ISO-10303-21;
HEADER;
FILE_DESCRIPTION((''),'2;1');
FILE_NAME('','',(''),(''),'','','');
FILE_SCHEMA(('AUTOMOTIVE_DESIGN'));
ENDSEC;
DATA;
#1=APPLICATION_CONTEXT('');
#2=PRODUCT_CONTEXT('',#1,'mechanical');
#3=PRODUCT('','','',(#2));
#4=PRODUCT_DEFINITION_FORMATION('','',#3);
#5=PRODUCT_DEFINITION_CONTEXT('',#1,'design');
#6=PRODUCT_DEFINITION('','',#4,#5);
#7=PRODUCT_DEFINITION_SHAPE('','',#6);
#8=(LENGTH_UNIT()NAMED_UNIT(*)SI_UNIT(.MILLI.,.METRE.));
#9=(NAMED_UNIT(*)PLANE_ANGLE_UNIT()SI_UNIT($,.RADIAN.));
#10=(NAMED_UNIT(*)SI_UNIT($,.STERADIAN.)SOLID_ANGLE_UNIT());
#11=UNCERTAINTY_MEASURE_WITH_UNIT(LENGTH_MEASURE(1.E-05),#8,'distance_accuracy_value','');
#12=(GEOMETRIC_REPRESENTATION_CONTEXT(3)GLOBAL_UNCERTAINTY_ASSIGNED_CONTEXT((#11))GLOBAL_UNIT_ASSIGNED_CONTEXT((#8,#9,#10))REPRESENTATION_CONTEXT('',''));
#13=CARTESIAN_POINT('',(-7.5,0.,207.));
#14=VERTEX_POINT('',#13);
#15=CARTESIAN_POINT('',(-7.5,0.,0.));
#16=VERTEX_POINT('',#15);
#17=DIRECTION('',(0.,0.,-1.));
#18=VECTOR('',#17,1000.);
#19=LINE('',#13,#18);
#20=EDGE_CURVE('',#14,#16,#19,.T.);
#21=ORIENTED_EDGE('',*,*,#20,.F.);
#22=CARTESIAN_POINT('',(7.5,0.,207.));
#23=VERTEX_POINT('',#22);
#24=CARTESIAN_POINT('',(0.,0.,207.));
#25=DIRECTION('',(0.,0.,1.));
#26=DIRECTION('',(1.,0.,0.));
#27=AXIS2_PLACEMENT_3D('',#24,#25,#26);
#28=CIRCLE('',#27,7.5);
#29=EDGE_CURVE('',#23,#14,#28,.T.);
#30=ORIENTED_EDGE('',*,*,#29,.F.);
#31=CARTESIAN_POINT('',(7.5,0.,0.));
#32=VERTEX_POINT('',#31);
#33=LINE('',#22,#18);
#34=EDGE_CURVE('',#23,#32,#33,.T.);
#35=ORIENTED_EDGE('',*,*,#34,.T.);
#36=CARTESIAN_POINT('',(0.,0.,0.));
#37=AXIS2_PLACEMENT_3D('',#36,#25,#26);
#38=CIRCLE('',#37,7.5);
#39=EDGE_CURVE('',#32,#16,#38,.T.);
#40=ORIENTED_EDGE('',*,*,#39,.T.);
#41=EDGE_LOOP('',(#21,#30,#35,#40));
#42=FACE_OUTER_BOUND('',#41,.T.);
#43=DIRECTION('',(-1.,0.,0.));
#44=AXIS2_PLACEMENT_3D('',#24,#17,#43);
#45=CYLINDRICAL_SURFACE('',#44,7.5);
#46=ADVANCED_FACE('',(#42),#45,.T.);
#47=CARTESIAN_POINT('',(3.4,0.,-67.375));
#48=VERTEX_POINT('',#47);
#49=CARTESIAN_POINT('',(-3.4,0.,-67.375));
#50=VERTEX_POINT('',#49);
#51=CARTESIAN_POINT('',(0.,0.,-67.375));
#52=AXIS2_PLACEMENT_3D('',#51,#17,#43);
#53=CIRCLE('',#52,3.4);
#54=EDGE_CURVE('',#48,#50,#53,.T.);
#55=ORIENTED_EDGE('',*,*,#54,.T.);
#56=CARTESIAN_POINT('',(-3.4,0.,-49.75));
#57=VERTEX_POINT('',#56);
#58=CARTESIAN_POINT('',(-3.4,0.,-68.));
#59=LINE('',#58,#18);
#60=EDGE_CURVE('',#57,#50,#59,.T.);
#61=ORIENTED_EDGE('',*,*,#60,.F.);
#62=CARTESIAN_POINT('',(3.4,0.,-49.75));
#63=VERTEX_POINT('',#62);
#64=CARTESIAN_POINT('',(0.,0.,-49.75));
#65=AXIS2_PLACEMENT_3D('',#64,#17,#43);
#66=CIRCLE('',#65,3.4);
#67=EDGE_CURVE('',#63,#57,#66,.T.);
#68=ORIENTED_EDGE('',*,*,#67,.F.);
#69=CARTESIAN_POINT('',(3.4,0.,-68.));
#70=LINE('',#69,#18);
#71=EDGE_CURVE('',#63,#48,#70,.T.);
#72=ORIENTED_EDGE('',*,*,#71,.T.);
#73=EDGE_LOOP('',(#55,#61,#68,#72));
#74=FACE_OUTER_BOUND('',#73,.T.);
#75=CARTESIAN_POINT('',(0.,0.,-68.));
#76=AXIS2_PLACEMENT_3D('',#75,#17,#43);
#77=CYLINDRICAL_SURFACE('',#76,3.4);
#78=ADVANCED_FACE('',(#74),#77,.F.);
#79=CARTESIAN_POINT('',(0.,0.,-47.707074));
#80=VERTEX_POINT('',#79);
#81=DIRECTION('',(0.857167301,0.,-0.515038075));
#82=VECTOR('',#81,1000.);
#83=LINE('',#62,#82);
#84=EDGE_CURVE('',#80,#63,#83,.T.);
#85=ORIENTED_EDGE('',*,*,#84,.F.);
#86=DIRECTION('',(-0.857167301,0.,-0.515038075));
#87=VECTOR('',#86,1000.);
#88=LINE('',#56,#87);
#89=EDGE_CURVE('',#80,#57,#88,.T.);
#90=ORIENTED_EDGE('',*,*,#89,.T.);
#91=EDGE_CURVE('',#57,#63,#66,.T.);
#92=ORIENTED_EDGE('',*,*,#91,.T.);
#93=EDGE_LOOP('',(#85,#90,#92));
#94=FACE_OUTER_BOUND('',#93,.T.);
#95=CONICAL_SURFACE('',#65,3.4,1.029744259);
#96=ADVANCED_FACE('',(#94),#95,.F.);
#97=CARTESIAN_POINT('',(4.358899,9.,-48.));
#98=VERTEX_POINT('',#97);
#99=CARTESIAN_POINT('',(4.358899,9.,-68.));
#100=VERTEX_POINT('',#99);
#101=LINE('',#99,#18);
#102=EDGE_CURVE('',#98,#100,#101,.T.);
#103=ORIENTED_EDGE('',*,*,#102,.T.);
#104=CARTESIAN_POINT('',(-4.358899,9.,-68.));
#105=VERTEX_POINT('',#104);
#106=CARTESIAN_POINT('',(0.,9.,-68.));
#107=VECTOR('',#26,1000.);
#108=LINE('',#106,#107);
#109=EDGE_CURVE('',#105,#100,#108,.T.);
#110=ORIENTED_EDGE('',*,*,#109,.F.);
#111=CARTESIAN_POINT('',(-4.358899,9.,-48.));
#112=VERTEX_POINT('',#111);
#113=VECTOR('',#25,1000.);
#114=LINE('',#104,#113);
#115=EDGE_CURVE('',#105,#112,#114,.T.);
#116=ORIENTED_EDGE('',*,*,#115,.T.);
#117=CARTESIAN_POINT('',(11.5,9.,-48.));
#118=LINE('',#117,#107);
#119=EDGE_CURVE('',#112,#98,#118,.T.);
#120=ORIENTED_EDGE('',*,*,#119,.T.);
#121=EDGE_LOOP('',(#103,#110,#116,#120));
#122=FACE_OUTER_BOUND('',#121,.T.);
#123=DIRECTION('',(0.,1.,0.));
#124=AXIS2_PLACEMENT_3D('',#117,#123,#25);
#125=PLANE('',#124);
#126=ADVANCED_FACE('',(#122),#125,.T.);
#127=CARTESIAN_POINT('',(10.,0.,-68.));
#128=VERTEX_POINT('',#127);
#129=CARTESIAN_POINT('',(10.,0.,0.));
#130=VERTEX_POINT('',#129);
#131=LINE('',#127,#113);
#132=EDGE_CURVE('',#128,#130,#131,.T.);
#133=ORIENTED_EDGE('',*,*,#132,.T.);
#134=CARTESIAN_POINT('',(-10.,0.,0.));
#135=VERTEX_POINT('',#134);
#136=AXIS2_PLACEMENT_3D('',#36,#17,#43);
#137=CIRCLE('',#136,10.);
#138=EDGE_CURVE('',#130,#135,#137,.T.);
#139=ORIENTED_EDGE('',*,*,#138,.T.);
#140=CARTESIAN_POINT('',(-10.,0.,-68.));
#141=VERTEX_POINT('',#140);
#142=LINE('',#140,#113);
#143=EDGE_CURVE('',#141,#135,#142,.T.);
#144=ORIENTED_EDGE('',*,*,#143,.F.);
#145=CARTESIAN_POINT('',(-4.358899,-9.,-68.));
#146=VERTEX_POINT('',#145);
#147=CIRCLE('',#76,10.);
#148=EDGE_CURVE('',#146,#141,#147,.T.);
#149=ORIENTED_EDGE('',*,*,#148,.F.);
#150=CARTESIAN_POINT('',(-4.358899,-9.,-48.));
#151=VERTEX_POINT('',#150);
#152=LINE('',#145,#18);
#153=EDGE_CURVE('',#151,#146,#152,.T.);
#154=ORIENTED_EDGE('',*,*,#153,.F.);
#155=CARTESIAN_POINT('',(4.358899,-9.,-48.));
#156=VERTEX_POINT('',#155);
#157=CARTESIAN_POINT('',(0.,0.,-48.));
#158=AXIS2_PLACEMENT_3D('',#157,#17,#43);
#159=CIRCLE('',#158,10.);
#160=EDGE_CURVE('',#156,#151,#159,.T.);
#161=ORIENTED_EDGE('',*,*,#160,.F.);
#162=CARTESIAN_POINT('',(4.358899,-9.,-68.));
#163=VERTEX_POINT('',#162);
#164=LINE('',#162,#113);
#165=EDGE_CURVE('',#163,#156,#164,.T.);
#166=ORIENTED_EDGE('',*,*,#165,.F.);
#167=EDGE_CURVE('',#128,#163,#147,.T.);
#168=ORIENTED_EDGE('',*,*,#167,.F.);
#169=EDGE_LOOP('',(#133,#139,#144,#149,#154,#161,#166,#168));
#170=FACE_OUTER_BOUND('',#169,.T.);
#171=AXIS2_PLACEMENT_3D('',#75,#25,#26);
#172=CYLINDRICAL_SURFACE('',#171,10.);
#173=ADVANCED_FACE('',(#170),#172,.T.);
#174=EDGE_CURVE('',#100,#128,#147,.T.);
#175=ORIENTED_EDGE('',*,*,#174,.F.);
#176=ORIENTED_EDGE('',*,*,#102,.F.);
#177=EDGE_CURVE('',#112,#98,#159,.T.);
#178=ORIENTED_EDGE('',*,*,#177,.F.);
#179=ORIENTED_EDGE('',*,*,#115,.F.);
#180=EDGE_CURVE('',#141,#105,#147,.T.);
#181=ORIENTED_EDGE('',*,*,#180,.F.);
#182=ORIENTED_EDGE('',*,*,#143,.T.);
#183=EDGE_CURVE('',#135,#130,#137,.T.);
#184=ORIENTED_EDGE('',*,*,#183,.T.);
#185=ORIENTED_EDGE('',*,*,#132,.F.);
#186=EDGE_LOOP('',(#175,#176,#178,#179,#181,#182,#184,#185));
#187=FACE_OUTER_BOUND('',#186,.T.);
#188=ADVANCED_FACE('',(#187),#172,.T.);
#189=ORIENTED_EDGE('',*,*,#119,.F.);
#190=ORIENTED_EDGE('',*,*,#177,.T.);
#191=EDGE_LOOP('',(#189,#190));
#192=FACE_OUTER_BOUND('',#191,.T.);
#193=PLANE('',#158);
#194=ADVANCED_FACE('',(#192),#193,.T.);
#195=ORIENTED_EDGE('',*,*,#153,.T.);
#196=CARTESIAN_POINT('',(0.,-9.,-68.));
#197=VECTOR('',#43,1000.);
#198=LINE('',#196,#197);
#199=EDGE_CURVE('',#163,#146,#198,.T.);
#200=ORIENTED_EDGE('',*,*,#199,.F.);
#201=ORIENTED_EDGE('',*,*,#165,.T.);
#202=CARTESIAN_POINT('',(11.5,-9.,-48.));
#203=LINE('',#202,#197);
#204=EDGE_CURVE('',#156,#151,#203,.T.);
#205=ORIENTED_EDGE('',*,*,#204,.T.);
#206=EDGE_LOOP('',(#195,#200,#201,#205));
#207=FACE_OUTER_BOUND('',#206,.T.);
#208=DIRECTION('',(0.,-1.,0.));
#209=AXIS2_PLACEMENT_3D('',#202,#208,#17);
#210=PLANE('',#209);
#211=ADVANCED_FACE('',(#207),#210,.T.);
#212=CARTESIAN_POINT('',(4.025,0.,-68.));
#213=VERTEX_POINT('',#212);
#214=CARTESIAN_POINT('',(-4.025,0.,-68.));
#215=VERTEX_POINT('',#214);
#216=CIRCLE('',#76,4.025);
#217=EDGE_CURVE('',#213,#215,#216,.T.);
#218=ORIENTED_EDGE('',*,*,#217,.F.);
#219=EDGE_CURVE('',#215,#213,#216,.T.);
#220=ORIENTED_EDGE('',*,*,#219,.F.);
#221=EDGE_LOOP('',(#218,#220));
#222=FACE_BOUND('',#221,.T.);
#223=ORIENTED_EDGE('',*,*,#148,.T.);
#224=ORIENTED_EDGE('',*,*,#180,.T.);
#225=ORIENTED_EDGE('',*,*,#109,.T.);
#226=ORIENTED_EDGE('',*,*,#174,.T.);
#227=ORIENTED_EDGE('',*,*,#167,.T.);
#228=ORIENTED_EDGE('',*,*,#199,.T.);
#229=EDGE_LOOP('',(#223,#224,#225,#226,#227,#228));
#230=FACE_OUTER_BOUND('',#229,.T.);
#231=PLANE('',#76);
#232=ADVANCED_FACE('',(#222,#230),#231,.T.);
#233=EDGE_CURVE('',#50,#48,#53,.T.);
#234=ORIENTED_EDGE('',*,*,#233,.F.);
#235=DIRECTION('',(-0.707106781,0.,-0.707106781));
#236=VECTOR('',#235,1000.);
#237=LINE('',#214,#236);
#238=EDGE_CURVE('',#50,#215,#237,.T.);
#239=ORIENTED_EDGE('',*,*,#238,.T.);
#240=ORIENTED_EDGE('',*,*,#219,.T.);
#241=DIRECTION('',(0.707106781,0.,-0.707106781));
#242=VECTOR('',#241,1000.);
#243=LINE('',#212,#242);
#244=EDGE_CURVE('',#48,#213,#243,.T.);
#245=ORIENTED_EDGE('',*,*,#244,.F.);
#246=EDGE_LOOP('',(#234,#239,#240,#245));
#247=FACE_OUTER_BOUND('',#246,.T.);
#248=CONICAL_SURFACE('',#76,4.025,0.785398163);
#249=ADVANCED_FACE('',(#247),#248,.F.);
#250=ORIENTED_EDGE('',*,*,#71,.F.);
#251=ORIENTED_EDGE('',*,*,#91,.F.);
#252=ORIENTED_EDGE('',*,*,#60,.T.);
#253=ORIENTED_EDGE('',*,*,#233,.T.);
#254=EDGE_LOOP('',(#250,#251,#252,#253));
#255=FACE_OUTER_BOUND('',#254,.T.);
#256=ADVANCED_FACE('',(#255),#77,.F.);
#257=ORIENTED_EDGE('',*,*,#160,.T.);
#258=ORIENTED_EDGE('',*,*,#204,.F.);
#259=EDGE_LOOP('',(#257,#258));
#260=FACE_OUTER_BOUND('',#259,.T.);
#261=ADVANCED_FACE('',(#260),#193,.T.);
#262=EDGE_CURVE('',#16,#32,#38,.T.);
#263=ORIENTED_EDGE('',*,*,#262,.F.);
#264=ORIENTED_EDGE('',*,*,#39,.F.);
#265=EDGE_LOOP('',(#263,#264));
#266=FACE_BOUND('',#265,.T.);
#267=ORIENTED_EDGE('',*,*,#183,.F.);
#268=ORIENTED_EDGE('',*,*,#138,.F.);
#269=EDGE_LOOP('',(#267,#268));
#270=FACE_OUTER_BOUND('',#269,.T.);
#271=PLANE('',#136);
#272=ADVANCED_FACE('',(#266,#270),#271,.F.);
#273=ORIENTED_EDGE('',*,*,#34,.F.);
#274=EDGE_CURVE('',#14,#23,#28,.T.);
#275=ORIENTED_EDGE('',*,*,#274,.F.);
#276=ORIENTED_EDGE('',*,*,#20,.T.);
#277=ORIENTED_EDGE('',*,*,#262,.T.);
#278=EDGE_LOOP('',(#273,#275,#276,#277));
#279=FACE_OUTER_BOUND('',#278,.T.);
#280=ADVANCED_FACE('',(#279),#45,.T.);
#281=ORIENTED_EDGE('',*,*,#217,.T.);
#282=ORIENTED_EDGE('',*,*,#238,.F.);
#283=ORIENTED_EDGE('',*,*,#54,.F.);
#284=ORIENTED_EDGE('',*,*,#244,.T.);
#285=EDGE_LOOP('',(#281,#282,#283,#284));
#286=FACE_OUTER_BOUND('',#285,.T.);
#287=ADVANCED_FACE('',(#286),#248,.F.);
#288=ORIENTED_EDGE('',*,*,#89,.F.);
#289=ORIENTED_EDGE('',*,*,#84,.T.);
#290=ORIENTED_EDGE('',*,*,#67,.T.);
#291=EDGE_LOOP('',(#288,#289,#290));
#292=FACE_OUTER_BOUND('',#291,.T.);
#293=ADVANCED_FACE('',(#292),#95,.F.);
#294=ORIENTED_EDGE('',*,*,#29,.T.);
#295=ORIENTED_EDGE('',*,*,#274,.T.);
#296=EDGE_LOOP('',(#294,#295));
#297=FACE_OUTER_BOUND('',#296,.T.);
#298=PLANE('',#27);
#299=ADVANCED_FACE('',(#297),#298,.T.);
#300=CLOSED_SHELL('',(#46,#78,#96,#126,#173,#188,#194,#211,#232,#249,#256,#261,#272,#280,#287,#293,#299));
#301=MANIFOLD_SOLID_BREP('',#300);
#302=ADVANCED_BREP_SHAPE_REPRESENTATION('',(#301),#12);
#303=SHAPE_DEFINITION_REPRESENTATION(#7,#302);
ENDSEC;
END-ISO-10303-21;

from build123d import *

# Parameters (mm, degrees)
SKETCH_1_R                   = 7.5
EXTRUDE_1_DEPTH              = 207
SKETCH_2_R                   = 10
EXTRUDE_2_DEPTH              = 68
SKETCH_3_OUTSIDE_W           = 77.29
SKETCH_3_OUTSIDE_H           = 77.29
SKETCH_3_OUTSIDE_W_2         = 23
SKETCH_3_OUTSIDE_H_2         = 18
CUT_EXTRUDE_1_DEPTH          = 20
HOLE_WIZARD_M8_1_D           = 6.8
HOLE_WIZARD_M8_1_DEPTH       = 18.25
HOLE_WIZARD_M8_1_CSINK_D     = 8.05
HOLE_WIZARD_M8_1_CSINK_ANGLE = 90
HOLE_WIZARD_M8_1_TIP         = 2.042926105


with BuildPart() as part:
    # 草图1 → 凸台-拉伸1 (new body)
    with BuildSketch(Plane.XY):
        Circle(SKETCH_1_R)
    extrude(amount=EXTRUDE_1_DEPTH)

    # 草图2 → 凸台-拉伸2 (add)
    with BuildSketch(Plane(origin=(0, 0, 0), x_dir=(-1, 0, 0), z_dir=(0, 0, -1))):
        Circle(SKETCH_2_R)
    extrude(amount=EXTRUDE_2_DEPTH)

    # 草图3 outside → 切除-拉伸1 (cut)
    with BuildSketch(Plane(origin=(0, 0, -68), x_dir=(-1, 0, 0), z_dir=(0, 0, -1))):
        Rectangle(SKETCH_3_OUTSIDE_W, SKETCH_3_OUTSIDE_H)
        Rectangle(SKETCH_3_OUTSIDE_W_2, SKETCH_3_OUTSIDE_H_2, mode=Mode.SUBTRACT)
    extrude(amount=-CUT_EXTRUDE_1_DEPTH, mode=Mode.SUBTRACT)

    # M8 螺纹孔1
    with Locations(Plane(origin=(0, 0, -68), x_dir=(-1, 0, 0), z_dir=(0, 0, -1))):
        with Locations((0, 0)):
            CounterSinkHole(HOLE_WIZARD_M8_1_D / 2, HOLE_WIZARD_M8_1_CSINK_D / 2, depth=HOLE_WIZARD_M8_1_DEPTH, counter_sink_angle=HOLE_WIZARD_M8_1_CSINK_ANGLE)
            with Locations((0, 0, -(HOLE_WIZARD_M8_1_DEPTH + HOLE_WIZARD_M8_1_TIP / 2))):  # 118° drill point
                Cone(0, HOLE_WIZARD_M8_1_D / 2, HOLE_WIZARD_M8_1_TIP, mode=Mode.SUBTRACT)


solid = part.part
